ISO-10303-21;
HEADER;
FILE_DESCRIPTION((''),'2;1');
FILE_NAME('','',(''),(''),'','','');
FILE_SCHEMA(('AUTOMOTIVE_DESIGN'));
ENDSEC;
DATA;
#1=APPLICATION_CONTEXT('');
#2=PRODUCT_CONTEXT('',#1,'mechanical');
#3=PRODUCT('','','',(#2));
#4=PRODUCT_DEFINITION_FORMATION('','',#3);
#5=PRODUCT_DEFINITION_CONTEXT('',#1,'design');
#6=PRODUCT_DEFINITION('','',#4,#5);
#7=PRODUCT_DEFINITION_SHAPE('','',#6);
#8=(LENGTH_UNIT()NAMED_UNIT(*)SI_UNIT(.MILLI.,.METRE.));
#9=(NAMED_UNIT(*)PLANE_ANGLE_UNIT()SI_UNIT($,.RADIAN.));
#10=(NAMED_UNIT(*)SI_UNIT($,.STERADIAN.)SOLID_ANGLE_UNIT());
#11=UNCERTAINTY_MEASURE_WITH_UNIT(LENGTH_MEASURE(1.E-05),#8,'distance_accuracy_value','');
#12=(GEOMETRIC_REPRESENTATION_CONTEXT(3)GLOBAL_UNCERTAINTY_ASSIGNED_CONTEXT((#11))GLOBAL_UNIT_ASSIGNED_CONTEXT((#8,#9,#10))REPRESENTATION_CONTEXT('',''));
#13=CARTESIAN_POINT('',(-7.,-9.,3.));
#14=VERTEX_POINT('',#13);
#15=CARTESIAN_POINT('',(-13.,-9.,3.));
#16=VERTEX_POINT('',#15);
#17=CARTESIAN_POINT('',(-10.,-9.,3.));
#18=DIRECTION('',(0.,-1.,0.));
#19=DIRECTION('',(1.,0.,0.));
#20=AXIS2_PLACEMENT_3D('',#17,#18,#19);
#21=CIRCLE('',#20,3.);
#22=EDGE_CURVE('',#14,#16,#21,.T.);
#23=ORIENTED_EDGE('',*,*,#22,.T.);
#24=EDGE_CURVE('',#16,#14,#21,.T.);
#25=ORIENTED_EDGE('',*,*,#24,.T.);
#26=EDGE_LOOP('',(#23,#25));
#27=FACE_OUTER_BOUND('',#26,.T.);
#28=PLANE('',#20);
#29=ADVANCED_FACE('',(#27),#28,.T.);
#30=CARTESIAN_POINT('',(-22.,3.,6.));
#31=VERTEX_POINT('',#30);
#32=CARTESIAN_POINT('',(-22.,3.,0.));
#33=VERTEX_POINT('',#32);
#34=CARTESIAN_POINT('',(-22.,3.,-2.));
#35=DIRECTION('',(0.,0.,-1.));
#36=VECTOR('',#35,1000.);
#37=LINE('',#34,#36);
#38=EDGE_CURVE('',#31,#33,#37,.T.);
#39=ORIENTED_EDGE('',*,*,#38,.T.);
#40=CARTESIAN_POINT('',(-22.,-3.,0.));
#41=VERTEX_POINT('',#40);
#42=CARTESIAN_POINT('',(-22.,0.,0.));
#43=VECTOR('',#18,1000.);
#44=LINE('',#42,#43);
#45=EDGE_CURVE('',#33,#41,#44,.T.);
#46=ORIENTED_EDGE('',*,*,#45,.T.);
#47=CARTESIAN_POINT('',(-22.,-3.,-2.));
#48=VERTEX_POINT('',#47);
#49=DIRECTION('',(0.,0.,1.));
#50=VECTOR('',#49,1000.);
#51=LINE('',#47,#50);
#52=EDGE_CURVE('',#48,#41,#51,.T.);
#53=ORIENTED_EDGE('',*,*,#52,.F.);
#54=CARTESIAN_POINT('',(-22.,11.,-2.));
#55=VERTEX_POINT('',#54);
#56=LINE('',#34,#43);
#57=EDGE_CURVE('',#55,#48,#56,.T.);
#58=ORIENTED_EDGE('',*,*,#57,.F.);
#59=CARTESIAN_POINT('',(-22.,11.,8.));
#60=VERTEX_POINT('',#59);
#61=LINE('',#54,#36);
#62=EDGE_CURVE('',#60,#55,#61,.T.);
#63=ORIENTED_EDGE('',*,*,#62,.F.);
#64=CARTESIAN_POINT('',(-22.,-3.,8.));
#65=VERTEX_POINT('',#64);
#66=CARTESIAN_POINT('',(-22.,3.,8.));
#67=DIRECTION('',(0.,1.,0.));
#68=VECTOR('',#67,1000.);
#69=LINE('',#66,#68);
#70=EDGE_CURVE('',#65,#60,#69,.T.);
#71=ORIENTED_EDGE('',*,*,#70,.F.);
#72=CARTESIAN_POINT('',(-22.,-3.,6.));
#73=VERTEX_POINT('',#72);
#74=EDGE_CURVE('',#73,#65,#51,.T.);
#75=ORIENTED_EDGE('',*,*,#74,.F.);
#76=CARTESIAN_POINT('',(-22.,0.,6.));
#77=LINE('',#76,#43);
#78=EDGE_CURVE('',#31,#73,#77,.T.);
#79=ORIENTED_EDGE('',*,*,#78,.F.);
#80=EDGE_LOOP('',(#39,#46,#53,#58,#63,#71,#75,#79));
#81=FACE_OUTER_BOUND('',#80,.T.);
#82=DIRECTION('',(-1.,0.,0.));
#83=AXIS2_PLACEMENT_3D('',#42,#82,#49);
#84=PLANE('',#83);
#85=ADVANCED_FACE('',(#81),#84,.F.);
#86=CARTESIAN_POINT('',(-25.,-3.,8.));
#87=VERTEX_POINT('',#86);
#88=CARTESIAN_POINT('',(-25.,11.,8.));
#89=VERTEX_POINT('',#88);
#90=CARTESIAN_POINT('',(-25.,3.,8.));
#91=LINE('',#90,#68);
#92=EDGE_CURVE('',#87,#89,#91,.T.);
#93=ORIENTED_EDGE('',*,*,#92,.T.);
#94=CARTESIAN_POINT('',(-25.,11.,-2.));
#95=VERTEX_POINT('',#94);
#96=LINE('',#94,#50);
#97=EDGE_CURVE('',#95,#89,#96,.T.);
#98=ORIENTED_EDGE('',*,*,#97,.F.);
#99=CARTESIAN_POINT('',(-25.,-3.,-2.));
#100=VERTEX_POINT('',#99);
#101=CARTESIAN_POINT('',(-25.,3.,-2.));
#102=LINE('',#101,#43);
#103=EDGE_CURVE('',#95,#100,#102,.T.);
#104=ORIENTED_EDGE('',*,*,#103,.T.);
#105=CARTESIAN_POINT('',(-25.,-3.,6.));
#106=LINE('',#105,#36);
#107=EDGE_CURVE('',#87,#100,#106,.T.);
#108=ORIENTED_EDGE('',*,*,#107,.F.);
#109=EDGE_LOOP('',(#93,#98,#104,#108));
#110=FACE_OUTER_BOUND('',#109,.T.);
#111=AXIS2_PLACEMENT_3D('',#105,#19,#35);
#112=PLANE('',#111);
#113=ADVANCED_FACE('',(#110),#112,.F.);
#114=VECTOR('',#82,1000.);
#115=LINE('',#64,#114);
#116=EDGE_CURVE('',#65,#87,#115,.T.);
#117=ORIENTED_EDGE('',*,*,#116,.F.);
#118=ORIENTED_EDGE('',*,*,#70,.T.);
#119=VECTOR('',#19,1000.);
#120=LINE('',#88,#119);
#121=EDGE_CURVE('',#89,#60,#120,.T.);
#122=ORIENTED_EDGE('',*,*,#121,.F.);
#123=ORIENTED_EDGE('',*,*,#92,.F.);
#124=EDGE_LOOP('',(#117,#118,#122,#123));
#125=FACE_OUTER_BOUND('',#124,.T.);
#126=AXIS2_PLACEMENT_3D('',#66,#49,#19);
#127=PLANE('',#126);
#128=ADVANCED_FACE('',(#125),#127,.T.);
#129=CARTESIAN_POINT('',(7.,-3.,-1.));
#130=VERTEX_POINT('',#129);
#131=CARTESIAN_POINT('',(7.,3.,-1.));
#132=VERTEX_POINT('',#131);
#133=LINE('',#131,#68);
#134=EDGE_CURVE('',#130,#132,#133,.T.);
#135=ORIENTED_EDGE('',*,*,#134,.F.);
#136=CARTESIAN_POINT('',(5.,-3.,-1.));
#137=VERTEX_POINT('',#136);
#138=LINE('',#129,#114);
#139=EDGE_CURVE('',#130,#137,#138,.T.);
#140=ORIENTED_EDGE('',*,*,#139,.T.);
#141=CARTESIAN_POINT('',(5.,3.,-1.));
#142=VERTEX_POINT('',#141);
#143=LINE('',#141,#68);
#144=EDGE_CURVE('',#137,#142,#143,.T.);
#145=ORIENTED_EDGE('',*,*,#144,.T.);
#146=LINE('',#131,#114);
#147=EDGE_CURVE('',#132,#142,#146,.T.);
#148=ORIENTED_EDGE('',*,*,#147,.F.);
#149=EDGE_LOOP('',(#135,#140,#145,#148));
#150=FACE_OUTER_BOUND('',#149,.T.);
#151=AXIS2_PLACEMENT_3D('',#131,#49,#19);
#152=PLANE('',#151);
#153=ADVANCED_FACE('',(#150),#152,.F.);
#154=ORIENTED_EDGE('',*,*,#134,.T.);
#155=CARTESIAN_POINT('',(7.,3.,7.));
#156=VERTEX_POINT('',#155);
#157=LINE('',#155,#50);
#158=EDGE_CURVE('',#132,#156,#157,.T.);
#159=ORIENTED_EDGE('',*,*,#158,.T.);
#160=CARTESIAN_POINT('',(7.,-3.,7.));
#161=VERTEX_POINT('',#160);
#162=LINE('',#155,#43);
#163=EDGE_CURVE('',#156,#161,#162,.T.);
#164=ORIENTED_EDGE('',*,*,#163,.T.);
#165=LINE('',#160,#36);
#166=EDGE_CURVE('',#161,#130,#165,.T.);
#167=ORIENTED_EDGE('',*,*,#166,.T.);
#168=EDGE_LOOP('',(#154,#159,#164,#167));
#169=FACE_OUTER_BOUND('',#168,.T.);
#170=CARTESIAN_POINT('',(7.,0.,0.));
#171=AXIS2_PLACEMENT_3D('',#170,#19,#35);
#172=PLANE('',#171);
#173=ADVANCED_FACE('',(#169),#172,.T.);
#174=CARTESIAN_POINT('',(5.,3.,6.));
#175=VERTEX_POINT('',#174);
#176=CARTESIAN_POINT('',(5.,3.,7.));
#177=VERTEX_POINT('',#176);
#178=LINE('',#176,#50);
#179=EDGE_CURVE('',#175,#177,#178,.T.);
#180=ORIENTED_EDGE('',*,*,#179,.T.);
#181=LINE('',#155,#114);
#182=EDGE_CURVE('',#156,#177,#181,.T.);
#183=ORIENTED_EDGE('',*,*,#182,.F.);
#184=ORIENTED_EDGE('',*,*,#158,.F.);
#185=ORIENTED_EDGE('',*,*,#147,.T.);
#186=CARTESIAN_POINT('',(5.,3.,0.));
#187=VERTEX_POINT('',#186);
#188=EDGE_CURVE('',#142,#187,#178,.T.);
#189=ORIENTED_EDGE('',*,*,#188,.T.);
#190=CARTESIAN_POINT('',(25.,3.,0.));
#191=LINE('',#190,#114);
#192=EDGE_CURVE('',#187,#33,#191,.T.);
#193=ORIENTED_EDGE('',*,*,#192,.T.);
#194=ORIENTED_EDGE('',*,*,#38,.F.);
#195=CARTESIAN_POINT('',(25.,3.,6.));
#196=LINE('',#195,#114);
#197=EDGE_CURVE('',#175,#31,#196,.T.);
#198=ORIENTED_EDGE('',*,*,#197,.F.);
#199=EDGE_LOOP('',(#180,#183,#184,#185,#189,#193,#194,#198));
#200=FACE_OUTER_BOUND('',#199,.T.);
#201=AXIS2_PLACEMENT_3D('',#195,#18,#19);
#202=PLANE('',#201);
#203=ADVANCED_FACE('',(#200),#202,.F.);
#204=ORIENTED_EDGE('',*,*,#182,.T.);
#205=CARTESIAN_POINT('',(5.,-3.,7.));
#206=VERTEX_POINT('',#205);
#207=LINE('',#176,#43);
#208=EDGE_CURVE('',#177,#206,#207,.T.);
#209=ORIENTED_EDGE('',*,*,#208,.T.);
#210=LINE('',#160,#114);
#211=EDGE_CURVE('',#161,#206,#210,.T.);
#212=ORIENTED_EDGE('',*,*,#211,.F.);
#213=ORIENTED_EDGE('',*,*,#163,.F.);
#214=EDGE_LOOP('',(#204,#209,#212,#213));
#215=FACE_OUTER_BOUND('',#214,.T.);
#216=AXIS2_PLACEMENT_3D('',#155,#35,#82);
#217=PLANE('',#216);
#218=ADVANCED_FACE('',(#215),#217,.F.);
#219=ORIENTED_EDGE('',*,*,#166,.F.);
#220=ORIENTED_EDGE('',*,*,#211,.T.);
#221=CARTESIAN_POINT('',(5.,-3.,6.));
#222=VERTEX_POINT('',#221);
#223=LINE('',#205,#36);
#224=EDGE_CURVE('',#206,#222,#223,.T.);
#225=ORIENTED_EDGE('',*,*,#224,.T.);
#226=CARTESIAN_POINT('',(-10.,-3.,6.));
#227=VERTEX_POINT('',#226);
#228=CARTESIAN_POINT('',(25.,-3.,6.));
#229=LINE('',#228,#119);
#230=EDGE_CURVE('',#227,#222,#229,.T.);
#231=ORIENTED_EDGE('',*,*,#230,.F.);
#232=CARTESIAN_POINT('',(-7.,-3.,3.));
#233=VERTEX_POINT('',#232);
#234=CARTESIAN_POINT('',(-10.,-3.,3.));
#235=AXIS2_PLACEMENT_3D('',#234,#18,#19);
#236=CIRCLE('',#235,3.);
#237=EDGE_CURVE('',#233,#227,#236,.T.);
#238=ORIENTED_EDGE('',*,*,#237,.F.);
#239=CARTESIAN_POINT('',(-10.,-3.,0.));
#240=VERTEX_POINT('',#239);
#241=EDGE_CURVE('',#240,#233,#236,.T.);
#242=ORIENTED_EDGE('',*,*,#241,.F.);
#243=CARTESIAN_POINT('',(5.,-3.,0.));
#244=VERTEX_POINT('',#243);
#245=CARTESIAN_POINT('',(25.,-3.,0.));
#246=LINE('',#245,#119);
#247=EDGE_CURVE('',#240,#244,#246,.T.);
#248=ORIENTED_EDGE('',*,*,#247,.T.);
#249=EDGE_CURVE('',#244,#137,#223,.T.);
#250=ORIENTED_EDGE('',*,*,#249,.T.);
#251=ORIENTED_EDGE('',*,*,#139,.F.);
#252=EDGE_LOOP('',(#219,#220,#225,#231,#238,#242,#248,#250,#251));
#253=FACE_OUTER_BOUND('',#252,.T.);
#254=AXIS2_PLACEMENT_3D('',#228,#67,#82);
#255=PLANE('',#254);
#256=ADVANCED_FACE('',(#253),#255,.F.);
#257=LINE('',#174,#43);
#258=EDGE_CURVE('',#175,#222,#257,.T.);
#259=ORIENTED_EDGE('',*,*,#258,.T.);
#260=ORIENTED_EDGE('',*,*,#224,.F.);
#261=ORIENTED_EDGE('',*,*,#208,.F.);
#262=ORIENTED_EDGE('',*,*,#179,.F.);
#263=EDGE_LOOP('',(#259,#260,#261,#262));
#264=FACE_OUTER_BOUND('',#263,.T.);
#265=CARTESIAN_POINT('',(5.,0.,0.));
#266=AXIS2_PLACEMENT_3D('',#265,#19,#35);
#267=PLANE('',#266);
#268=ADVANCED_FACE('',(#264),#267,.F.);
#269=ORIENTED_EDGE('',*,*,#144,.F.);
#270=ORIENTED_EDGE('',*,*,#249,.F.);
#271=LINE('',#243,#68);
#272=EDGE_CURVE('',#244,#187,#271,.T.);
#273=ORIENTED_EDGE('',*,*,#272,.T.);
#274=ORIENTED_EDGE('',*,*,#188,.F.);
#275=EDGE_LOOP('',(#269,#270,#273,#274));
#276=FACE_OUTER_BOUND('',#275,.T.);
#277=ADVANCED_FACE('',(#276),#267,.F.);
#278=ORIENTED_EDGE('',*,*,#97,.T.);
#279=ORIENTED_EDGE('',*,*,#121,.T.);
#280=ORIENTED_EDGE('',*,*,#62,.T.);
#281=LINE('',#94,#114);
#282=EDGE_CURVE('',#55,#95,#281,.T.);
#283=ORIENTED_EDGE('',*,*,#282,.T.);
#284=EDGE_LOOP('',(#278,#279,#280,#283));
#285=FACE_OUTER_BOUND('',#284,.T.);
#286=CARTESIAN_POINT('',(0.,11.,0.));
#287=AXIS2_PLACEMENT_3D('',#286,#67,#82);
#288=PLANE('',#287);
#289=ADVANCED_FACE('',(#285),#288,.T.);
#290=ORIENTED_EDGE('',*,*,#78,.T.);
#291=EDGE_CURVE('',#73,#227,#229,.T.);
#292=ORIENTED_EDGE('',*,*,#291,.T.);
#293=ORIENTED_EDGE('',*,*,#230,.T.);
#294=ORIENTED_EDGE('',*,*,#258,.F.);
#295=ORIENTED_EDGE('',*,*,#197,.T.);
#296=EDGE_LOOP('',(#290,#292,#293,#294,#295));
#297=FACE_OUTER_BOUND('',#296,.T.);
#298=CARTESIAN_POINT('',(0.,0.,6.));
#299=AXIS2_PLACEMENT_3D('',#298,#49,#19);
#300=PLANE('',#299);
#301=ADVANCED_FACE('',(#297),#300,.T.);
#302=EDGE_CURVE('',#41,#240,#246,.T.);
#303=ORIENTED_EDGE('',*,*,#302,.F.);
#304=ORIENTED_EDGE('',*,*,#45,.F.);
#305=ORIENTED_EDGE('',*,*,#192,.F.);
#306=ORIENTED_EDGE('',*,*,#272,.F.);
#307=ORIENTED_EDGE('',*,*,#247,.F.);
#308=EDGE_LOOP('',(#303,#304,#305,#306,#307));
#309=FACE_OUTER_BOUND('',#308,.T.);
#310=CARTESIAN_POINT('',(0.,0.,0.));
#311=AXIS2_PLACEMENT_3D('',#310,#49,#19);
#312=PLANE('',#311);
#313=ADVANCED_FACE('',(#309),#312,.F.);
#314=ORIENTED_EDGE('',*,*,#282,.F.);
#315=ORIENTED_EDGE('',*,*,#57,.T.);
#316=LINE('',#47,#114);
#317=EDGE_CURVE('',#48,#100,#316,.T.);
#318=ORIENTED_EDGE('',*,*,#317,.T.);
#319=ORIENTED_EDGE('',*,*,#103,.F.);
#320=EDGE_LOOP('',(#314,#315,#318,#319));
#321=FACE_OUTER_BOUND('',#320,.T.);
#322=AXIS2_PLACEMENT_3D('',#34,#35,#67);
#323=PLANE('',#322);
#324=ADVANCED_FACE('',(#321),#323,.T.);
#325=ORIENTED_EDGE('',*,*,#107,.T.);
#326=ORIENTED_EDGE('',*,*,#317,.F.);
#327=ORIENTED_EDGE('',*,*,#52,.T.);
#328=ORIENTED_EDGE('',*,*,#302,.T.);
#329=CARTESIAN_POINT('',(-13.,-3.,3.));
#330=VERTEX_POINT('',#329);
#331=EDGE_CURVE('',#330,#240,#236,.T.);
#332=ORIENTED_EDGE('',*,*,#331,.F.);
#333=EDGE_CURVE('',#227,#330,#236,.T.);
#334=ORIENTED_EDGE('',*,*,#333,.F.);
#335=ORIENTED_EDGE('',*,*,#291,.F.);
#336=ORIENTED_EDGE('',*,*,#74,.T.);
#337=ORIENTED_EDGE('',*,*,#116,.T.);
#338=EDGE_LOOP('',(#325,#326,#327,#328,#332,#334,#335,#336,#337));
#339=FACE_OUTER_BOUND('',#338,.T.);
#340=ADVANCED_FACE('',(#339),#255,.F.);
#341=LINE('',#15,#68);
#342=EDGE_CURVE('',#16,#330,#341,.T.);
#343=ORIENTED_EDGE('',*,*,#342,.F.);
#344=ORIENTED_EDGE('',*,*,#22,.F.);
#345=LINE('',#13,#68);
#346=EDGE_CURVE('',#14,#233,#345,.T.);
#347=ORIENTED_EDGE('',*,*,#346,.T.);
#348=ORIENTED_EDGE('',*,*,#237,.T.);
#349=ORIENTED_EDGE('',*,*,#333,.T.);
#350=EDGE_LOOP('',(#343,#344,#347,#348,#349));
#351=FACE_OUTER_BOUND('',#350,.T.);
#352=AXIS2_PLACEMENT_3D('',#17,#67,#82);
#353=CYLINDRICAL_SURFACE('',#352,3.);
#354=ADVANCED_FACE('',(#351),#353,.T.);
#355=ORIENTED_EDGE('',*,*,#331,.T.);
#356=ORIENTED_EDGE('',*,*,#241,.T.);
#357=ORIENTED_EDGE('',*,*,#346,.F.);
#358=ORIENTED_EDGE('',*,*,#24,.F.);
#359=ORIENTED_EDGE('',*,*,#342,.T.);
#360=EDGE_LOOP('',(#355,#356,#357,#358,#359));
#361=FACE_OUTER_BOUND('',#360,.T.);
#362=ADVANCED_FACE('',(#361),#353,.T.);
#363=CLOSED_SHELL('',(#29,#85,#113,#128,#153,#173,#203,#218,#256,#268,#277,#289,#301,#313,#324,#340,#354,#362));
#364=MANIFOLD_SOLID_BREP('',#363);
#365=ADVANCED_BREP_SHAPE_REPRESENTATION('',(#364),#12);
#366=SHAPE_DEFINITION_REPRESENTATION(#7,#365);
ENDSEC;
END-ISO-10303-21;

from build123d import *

# Parameters (mm, degrees)
SKETCH1_W           = 50
SKETCH1_H           = 6
BOSS_EXTRUDE1_DEPTH = 6
SKETCH2_R           = 3
BOSS_EXTRUDE2_DEPTH = 6
SKETCH3_W           = 10
SKETCH3_H           = 6
BOSS_EXTRUDE3_DEPTH = 3
SKETCH4_W           = 6
SKETCH4_H           = 6
CUT_EXTRUDE1_DEPTH  = 20
SKETCH5_W           = 8
SKETCH5_H           = 6
BOSS_EXTRUDE4_DEPTH = 2
SKETCH6_W           = 3
SKETCH6_H           = 10
BOSS_EXTRUDE5_DEPTH = 8


with BuildPart() as part:
    # Sketch1 → Boss-Extrude1 (new body)
    with BuildSketch(Plane.XY):
        Rectangle(SKETCH1_W, SKETCH1_H)
    extrude(amount=BOSS_EXTRUDE1_DEPTH)

    # Sketch2 → Boss-Extrude2 (add)
    with BuildSketch(Plane.XZ.offset(3)):
        with Locations(Location((-10, 3, 0), (0, 0, 270))):
            Circle(SKETCH2_R)
    extrude(amount=BOSS_EXTRUDE2_DEPTH)

    # Sketch3 → Boss-Extrude3 (add)
    with BuildSketch(Plane.ZY.offset(25)):
        with Locations((3, 0)):
            Rectangle(SKETCH3_W, SKETCH3_H)
    extrude(amount=-BOSS_EXTRUDE3_DEPTH)

    # Sketch4 → Cut-Extrude1 (cut)
    with BuildSketch(Plane(origin=(25, 0, 0), x_dir=(0, 0, -1), z_dir=(1, 0, 0))):
        with Locations((-3, 0)):
            Rectangle(SKETCH4_W, SKETCH4_H)
    extrude(amount=-CUT_EXTRUDE1_DEPTH, mode=Mode.SUBTRACT)

    # Sketch5 → Boss-Extrude4 (add)
    with BuildSketch(Plane(origin=(5, 0, 0), x_dir=(0, 0, -1), z_dir=(1, 0, 0))):
        with Locations((-3, 0)):
            Rectangle(SKETCH5_W, SKETCH5_H)
    extrude(amount=BOSS_EXTRUDE4_DEPTH)

    # Sketch6 → Boss-Extrude5 (add)
    with BuildSketch(Plane(origin=(0, 3, 0), x_dir=(1, 0, 0), z_dir=(0, 1, 0))):
        with Locations((-23.5, -3)):
            Rectangle(SKETCH6_W, SKETCH6_H)
    extrude(amount=BOSS_EXTRUDE5_DEPTH)


solid = part.part
